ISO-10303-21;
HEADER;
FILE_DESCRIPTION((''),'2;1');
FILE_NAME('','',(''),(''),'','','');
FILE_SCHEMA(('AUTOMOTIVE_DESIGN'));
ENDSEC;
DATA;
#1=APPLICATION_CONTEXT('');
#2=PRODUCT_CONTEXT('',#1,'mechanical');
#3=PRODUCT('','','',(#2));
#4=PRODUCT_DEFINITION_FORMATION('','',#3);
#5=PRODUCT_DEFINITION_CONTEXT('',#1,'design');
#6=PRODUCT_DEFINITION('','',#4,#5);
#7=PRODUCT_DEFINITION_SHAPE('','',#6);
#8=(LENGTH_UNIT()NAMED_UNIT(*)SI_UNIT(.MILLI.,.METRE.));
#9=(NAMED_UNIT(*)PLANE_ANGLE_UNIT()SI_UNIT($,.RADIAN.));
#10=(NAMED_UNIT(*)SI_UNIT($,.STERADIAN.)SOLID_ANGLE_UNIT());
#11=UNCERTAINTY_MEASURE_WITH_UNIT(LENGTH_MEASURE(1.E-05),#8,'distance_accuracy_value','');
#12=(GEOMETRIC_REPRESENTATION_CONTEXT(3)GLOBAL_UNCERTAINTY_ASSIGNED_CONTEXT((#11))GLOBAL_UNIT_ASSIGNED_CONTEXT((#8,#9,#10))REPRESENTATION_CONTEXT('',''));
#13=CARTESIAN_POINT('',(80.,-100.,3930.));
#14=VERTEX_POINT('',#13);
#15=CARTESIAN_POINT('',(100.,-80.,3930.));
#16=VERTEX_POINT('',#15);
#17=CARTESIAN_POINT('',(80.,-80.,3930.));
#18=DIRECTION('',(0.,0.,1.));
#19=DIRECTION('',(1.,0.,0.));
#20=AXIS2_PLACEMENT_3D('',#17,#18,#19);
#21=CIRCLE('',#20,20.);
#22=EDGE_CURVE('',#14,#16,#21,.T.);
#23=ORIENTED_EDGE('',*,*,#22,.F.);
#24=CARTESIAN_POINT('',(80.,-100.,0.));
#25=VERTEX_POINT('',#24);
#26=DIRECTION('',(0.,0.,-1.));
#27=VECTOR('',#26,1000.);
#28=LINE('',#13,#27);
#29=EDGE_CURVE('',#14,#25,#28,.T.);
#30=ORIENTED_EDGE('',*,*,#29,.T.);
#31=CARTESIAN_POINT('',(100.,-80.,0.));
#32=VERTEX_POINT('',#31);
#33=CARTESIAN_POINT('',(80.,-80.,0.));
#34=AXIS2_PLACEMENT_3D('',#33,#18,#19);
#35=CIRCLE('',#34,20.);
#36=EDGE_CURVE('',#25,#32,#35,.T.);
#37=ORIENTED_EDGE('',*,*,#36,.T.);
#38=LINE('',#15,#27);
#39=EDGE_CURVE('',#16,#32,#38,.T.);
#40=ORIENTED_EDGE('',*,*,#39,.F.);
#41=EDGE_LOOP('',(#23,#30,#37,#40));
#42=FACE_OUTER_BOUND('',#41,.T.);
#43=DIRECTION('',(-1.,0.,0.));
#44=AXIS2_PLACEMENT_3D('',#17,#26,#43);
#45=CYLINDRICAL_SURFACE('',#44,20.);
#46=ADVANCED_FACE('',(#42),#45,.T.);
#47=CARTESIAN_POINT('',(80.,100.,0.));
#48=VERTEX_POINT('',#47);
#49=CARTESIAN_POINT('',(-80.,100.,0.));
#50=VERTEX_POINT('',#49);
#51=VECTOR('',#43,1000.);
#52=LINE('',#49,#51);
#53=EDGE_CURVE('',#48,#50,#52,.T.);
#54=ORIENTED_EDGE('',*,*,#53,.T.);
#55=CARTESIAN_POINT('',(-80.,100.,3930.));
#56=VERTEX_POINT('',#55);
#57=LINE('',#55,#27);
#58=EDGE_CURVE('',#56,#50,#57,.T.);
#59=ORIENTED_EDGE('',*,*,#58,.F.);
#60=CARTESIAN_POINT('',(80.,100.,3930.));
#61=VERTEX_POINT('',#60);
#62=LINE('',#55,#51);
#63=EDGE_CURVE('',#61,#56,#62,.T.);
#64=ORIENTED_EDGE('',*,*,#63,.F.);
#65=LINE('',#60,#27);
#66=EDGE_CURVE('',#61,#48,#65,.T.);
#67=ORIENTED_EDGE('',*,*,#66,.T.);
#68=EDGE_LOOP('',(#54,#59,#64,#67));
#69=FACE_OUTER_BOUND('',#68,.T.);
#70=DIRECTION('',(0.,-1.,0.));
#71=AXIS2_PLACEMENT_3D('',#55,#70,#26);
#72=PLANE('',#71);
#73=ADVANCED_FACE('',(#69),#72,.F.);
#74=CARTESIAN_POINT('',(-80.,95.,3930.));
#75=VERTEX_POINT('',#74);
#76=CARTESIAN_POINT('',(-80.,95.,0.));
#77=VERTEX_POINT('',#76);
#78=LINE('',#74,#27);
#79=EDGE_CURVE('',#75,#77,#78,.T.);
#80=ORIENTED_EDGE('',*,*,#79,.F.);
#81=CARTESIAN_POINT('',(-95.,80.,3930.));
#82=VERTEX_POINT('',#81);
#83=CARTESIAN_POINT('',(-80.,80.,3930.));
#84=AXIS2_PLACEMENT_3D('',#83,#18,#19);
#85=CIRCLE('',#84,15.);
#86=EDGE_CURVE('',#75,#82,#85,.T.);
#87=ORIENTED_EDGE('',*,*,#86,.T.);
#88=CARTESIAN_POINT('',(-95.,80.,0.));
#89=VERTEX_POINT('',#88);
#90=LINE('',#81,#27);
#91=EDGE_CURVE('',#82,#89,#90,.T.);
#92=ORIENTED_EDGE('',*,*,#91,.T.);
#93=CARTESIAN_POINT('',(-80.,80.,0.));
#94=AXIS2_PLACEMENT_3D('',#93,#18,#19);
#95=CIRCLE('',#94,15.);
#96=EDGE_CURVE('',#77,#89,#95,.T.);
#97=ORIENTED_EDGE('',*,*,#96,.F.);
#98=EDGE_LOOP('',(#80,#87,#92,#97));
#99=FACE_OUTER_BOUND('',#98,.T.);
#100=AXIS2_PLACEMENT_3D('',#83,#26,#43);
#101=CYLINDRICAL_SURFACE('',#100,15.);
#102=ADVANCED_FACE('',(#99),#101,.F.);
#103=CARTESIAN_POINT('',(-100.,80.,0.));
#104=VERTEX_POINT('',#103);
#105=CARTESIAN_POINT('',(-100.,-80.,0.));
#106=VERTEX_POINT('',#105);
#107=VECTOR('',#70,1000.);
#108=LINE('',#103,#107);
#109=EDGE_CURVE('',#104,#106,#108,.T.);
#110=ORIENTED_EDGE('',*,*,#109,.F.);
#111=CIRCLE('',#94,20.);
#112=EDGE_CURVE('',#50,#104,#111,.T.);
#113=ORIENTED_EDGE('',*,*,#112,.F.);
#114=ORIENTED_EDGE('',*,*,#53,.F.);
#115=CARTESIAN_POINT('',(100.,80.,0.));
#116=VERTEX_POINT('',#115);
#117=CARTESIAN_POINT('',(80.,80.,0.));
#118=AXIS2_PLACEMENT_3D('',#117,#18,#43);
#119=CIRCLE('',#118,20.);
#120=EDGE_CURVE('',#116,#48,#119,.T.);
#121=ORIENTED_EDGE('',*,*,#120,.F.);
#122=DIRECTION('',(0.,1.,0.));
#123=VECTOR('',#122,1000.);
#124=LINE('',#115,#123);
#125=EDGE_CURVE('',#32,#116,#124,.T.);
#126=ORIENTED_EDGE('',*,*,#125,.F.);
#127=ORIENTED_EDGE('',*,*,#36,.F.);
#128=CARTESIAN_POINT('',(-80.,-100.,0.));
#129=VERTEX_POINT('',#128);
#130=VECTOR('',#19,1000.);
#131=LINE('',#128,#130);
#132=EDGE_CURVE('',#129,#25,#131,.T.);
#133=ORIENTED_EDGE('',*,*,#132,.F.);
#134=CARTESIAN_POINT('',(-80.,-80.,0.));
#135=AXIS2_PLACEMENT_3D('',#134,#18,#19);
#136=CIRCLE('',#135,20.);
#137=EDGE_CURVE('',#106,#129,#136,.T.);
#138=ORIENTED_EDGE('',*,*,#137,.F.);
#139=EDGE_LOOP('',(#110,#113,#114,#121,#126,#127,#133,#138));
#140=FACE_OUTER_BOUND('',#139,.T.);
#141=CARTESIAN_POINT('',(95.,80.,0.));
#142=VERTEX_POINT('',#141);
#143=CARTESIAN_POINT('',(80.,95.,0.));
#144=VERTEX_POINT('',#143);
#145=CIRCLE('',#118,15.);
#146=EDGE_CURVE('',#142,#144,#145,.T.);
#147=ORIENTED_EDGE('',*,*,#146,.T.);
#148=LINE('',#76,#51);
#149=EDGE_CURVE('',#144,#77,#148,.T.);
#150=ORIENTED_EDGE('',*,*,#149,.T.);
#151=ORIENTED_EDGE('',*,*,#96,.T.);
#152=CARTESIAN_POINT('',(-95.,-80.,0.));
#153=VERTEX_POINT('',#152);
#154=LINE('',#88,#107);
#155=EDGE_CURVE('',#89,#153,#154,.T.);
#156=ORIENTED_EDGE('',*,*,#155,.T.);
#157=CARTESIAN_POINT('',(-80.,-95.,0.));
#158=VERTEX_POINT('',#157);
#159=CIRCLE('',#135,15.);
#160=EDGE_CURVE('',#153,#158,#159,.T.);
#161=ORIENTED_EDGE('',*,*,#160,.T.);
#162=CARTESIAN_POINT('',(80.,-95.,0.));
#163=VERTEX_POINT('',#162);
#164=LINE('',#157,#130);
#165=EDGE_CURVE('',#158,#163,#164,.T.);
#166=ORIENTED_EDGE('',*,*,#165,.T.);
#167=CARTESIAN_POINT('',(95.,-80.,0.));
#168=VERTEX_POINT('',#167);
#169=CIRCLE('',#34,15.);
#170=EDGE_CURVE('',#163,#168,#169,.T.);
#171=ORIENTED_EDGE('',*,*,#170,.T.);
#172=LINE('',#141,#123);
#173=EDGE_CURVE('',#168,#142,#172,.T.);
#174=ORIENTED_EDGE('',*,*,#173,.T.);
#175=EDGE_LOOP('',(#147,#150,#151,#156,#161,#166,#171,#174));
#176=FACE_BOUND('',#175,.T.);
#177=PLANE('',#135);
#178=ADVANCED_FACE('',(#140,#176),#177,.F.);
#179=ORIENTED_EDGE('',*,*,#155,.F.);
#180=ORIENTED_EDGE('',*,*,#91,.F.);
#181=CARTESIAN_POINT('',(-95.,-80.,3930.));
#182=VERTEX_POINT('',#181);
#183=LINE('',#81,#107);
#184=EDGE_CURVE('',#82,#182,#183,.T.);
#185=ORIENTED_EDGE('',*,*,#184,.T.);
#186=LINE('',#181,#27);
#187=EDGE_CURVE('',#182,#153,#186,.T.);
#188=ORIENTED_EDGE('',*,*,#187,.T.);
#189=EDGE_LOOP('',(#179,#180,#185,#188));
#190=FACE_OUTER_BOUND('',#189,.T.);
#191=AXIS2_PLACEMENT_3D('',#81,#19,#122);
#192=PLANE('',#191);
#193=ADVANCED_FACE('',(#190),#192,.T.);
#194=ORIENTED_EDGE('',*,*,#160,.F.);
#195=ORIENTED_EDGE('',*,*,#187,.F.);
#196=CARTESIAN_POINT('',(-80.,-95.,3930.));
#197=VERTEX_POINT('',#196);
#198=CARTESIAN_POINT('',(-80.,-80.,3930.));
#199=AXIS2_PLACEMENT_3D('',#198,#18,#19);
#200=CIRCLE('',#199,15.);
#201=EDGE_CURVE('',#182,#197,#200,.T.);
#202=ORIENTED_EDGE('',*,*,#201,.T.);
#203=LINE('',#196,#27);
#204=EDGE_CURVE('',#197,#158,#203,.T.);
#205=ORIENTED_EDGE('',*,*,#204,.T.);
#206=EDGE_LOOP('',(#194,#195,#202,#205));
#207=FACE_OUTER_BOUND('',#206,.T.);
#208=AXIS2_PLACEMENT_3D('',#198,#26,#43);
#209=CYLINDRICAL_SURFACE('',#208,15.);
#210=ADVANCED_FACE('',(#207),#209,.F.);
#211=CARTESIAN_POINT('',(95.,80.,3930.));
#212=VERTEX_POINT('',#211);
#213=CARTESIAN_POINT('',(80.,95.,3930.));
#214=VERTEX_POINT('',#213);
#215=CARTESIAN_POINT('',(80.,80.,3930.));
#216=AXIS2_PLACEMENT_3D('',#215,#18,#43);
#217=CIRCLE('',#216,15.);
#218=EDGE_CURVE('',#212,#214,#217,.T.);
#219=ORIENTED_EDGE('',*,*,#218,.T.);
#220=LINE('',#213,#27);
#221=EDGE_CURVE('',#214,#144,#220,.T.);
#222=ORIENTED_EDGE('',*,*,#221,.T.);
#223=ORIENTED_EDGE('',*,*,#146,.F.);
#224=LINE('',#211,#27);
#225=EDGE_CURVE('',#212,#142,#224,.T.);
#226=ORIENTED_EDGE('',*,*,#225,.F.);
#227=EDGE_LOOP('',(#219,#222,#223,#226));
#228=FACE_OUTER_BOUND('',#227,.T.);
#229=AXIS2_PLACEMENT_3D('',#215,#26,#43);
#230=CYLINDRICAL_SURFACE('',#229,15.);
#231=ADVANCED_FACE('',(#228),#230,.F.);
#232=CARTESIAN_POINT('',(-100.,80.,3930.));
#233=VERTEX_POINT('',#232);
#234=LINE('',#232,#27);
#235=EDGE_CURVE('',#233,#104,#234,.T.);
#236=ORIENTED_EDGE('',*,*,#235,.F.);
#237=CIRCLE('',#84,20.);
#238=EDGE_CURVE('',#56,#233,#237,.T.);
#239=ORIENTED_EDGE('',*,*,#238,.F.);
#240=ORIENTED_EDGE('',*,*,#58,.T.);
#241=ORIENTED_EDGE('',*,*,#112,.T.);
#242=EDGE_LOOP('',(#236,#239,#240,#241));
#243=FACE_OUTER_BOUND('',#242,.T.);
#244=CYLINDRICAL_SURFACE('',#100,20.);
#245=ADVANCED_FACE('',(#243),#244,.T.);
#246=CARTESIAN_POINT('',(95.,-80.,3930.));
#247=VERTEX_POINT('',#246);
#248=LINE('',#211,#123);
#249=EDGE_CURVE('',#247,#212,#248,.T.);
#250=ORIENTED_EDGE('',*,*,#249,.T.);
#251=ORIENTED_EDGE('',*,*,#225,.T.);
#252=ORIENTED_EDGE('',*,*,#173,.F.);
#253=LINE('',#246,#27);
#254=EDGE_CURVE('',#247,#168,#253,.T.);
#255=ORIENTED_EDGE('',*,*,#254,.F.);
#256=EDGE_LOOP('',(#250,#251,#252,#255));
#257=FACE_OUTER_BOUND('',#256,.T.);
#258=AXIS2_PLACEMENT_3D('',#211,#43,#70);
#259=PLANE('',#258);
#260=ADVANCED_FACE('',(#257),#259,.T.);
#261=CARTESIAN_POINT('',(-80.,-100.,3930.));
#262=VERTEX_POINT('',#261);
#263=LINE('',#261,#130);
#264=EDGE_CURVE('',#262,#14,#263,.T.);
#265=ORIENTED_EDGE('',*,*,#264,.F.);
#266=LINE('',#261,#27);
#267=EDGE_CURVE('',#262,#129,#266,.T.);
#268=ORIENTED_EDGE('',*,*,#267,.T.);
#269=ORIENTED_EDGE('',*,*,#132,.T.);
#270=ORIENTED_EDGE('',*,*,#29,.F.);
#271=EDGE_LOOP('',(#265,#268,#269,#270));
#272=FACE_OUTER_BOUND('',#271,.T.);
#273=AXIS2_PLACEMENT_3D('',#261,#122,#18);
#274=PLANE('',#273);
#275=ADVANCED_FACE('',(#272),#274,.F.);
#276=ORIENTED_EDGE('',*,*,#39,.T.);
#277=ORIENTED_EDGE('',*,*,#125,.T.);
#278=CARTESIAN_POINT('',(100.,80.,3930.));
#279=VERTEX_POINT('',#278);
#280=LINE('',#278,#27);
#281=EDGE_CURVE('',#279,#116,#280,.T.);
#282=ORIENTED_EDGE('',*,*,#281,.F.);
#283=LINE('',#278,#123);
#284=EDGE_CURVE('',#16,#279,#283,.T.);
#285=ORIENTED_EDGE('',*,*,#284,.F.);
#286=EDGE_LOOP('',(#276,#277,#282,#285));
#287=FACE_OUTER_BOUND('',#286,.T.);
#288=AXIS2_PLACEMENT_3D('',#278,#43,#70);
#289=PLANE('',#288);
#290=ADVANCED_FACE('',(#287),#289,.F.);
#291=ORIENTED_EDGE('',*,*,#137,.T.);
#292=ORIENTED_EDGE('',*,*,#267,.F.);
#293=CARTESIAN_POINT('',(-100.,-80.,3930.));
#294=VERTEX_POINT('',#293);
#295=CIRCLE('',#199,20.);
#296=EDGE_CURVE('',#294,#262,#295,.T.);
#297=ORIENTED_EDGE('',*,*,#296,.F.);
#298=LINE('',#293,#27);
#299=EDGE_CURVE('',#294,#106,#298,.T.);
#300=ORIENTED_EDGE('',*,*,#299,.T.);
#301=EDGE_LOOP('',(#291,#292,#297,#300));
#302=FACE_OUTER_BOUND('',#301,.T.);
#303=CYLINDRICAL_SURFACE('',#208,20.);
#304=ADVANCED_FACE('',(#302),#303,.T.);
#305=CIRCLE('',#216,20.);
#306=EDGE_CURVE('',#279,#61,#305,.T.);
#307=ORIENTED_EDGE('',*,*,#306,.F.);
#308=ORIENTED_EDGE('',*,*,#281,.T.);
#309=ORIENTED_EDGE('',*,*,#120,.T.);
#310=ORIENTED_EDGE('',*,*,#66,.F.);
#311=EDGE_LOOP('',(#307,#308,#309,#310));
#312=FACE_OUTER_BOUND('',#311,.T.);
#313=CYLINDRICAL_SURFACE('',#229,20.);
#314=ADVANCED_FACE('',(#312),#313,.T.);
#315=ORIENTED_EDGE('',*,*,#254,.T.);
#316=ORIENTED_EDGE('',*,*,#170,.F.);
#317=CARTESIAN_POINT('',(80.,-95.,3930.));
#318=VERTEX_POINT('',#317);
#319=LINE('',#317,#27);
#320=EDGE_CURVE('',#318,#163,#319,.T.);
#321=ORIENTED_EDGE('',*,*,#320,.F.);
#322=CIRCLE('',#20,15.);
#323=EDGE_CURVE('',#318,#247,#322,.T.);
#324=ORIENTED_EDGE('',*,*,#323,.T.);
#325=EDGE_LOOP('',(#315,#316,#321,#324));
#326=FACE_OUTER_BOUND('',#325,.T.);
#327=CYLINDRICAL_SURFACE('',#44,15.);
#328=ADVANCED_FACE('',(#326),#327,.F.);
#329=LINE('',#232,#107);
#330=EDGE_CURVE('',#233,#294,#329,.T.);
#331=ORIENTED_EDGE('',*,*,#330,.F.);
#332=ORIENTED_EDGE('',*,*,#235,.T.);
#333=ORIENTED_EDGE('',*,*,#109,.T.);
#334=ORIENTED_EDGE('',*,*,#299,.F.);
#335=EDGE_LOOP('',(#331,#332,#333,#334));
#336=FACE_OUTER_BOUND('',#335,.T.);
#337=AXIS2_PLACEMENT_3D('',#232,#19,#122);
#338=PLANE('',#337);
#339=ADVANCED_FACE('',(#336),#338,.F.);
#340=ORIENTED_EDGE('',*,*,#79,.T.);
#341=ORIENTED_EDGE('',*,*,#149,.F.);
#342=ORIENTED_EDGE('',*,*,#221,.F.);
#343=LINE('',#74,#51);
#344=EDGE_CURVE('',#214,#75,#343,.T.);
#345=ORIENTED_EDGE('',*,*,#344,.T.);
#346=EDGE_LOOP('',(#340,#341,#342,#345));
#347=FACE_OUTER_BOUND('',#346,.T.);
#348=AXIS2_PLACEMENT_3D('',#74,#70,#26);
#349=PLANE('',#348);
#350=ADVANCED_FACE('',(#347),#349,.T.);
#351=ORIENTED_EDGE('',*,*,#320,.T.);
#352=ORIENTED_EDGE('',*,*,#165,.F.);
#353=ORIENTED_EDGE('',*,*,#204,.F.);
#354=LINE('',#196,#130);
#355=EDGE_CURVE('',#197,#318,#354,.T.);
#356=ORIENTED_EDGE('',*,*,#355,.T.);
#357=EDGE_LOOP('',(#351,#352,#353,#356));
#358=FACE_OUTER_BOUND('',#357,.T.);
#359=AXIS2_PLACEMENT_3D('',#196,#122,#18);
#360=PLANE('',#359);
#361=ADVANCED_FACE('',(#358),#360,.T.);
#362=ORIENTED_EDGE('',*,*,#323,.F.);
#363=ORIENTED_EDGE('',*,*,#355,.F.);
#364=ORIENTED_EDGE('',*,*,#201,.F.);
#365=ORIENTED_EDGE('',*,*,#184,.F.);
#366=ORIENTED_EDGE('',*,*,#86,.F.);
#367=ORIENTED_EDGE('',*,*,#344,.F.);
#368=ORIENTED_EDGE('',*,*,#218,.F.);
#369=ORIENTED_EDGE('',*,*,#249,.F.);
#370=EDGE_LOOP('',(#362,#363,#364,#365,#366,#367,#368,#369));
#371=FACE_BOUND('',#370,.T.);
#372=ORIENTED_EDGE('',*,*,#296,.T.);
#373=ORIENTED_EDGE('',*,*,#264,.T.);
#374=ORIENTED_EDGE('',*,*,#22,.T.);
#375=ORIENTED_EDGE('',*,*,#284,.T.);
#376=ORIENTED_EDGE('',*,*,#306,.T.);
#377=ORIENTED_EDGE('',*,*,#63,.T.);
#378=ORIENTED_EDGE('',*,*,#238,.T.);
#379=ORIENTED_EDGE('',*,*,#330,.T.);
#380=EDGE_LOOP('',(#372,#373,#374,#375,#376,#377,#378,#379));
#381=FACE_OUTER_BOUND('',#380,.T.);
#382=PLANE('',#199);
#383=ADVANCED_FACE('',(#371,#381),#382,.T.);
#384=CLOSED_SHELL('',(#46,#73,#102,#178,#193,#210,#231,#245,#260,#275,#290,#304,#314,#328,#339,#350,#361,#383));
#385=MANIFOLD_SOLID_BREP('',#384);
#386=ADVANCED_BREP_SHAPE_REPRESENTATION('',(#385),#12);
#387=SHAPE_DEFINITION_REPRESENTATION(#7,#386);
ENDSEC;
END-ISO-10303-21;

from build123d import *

# Parameters (mm, degrees)
BOSS_EXTRUDE1_DEPTH = 3930


with BuildPart() as part:
    # Sketch1 → Boss-Extrude1 (new body)
    with BuildSketch(Plane.XY):
        with BuildLine():
            Line((-80, 100), (80, 100))
            ThreePointArc((80, 100), (94.142135624, 94.142135624), (100, 80))
            Line((100, 80), (100, -80))
            ThreePointArc((100, -80), (94.142135624, -94.142135624), (80, -100))
            Line((80, -100), (-80, -100))
            ThreePointArc((-80, -100), (-94.142135624, -94.142135624), (-100, -80))
            Line((-100, -80), (-100, 80))
            ThreePointArc((-100, 80), (-94.142135624, 94.142135624), (-80, 100))
        make_face()
        with BuildLine():
            Line((-95, 80), (-95, -80))
            ThreePointArc((-95, -80), (-90.606601718, -90.606601718), (-80, -95))
            Line((-80, -95), (80, -95))
            ThreePointArc((80, -95), (90.606601718, -90.606601718), (95, -80))
            Line((95, -80), (95, 80))
            ThreePointArc((95, 80), (90.606601718, 90.606601718), (80, 95))
            Line((80, 95), (-80, 95))
            ThreePointArc((-80, 95), (-90.606601718, 90.606601718), (-95, 80))
        make_face(mode=Mode.SUBTRACT)
    extrude(amount=BOSS_EXTRUDE1_DEPTH)


solid = part.part
